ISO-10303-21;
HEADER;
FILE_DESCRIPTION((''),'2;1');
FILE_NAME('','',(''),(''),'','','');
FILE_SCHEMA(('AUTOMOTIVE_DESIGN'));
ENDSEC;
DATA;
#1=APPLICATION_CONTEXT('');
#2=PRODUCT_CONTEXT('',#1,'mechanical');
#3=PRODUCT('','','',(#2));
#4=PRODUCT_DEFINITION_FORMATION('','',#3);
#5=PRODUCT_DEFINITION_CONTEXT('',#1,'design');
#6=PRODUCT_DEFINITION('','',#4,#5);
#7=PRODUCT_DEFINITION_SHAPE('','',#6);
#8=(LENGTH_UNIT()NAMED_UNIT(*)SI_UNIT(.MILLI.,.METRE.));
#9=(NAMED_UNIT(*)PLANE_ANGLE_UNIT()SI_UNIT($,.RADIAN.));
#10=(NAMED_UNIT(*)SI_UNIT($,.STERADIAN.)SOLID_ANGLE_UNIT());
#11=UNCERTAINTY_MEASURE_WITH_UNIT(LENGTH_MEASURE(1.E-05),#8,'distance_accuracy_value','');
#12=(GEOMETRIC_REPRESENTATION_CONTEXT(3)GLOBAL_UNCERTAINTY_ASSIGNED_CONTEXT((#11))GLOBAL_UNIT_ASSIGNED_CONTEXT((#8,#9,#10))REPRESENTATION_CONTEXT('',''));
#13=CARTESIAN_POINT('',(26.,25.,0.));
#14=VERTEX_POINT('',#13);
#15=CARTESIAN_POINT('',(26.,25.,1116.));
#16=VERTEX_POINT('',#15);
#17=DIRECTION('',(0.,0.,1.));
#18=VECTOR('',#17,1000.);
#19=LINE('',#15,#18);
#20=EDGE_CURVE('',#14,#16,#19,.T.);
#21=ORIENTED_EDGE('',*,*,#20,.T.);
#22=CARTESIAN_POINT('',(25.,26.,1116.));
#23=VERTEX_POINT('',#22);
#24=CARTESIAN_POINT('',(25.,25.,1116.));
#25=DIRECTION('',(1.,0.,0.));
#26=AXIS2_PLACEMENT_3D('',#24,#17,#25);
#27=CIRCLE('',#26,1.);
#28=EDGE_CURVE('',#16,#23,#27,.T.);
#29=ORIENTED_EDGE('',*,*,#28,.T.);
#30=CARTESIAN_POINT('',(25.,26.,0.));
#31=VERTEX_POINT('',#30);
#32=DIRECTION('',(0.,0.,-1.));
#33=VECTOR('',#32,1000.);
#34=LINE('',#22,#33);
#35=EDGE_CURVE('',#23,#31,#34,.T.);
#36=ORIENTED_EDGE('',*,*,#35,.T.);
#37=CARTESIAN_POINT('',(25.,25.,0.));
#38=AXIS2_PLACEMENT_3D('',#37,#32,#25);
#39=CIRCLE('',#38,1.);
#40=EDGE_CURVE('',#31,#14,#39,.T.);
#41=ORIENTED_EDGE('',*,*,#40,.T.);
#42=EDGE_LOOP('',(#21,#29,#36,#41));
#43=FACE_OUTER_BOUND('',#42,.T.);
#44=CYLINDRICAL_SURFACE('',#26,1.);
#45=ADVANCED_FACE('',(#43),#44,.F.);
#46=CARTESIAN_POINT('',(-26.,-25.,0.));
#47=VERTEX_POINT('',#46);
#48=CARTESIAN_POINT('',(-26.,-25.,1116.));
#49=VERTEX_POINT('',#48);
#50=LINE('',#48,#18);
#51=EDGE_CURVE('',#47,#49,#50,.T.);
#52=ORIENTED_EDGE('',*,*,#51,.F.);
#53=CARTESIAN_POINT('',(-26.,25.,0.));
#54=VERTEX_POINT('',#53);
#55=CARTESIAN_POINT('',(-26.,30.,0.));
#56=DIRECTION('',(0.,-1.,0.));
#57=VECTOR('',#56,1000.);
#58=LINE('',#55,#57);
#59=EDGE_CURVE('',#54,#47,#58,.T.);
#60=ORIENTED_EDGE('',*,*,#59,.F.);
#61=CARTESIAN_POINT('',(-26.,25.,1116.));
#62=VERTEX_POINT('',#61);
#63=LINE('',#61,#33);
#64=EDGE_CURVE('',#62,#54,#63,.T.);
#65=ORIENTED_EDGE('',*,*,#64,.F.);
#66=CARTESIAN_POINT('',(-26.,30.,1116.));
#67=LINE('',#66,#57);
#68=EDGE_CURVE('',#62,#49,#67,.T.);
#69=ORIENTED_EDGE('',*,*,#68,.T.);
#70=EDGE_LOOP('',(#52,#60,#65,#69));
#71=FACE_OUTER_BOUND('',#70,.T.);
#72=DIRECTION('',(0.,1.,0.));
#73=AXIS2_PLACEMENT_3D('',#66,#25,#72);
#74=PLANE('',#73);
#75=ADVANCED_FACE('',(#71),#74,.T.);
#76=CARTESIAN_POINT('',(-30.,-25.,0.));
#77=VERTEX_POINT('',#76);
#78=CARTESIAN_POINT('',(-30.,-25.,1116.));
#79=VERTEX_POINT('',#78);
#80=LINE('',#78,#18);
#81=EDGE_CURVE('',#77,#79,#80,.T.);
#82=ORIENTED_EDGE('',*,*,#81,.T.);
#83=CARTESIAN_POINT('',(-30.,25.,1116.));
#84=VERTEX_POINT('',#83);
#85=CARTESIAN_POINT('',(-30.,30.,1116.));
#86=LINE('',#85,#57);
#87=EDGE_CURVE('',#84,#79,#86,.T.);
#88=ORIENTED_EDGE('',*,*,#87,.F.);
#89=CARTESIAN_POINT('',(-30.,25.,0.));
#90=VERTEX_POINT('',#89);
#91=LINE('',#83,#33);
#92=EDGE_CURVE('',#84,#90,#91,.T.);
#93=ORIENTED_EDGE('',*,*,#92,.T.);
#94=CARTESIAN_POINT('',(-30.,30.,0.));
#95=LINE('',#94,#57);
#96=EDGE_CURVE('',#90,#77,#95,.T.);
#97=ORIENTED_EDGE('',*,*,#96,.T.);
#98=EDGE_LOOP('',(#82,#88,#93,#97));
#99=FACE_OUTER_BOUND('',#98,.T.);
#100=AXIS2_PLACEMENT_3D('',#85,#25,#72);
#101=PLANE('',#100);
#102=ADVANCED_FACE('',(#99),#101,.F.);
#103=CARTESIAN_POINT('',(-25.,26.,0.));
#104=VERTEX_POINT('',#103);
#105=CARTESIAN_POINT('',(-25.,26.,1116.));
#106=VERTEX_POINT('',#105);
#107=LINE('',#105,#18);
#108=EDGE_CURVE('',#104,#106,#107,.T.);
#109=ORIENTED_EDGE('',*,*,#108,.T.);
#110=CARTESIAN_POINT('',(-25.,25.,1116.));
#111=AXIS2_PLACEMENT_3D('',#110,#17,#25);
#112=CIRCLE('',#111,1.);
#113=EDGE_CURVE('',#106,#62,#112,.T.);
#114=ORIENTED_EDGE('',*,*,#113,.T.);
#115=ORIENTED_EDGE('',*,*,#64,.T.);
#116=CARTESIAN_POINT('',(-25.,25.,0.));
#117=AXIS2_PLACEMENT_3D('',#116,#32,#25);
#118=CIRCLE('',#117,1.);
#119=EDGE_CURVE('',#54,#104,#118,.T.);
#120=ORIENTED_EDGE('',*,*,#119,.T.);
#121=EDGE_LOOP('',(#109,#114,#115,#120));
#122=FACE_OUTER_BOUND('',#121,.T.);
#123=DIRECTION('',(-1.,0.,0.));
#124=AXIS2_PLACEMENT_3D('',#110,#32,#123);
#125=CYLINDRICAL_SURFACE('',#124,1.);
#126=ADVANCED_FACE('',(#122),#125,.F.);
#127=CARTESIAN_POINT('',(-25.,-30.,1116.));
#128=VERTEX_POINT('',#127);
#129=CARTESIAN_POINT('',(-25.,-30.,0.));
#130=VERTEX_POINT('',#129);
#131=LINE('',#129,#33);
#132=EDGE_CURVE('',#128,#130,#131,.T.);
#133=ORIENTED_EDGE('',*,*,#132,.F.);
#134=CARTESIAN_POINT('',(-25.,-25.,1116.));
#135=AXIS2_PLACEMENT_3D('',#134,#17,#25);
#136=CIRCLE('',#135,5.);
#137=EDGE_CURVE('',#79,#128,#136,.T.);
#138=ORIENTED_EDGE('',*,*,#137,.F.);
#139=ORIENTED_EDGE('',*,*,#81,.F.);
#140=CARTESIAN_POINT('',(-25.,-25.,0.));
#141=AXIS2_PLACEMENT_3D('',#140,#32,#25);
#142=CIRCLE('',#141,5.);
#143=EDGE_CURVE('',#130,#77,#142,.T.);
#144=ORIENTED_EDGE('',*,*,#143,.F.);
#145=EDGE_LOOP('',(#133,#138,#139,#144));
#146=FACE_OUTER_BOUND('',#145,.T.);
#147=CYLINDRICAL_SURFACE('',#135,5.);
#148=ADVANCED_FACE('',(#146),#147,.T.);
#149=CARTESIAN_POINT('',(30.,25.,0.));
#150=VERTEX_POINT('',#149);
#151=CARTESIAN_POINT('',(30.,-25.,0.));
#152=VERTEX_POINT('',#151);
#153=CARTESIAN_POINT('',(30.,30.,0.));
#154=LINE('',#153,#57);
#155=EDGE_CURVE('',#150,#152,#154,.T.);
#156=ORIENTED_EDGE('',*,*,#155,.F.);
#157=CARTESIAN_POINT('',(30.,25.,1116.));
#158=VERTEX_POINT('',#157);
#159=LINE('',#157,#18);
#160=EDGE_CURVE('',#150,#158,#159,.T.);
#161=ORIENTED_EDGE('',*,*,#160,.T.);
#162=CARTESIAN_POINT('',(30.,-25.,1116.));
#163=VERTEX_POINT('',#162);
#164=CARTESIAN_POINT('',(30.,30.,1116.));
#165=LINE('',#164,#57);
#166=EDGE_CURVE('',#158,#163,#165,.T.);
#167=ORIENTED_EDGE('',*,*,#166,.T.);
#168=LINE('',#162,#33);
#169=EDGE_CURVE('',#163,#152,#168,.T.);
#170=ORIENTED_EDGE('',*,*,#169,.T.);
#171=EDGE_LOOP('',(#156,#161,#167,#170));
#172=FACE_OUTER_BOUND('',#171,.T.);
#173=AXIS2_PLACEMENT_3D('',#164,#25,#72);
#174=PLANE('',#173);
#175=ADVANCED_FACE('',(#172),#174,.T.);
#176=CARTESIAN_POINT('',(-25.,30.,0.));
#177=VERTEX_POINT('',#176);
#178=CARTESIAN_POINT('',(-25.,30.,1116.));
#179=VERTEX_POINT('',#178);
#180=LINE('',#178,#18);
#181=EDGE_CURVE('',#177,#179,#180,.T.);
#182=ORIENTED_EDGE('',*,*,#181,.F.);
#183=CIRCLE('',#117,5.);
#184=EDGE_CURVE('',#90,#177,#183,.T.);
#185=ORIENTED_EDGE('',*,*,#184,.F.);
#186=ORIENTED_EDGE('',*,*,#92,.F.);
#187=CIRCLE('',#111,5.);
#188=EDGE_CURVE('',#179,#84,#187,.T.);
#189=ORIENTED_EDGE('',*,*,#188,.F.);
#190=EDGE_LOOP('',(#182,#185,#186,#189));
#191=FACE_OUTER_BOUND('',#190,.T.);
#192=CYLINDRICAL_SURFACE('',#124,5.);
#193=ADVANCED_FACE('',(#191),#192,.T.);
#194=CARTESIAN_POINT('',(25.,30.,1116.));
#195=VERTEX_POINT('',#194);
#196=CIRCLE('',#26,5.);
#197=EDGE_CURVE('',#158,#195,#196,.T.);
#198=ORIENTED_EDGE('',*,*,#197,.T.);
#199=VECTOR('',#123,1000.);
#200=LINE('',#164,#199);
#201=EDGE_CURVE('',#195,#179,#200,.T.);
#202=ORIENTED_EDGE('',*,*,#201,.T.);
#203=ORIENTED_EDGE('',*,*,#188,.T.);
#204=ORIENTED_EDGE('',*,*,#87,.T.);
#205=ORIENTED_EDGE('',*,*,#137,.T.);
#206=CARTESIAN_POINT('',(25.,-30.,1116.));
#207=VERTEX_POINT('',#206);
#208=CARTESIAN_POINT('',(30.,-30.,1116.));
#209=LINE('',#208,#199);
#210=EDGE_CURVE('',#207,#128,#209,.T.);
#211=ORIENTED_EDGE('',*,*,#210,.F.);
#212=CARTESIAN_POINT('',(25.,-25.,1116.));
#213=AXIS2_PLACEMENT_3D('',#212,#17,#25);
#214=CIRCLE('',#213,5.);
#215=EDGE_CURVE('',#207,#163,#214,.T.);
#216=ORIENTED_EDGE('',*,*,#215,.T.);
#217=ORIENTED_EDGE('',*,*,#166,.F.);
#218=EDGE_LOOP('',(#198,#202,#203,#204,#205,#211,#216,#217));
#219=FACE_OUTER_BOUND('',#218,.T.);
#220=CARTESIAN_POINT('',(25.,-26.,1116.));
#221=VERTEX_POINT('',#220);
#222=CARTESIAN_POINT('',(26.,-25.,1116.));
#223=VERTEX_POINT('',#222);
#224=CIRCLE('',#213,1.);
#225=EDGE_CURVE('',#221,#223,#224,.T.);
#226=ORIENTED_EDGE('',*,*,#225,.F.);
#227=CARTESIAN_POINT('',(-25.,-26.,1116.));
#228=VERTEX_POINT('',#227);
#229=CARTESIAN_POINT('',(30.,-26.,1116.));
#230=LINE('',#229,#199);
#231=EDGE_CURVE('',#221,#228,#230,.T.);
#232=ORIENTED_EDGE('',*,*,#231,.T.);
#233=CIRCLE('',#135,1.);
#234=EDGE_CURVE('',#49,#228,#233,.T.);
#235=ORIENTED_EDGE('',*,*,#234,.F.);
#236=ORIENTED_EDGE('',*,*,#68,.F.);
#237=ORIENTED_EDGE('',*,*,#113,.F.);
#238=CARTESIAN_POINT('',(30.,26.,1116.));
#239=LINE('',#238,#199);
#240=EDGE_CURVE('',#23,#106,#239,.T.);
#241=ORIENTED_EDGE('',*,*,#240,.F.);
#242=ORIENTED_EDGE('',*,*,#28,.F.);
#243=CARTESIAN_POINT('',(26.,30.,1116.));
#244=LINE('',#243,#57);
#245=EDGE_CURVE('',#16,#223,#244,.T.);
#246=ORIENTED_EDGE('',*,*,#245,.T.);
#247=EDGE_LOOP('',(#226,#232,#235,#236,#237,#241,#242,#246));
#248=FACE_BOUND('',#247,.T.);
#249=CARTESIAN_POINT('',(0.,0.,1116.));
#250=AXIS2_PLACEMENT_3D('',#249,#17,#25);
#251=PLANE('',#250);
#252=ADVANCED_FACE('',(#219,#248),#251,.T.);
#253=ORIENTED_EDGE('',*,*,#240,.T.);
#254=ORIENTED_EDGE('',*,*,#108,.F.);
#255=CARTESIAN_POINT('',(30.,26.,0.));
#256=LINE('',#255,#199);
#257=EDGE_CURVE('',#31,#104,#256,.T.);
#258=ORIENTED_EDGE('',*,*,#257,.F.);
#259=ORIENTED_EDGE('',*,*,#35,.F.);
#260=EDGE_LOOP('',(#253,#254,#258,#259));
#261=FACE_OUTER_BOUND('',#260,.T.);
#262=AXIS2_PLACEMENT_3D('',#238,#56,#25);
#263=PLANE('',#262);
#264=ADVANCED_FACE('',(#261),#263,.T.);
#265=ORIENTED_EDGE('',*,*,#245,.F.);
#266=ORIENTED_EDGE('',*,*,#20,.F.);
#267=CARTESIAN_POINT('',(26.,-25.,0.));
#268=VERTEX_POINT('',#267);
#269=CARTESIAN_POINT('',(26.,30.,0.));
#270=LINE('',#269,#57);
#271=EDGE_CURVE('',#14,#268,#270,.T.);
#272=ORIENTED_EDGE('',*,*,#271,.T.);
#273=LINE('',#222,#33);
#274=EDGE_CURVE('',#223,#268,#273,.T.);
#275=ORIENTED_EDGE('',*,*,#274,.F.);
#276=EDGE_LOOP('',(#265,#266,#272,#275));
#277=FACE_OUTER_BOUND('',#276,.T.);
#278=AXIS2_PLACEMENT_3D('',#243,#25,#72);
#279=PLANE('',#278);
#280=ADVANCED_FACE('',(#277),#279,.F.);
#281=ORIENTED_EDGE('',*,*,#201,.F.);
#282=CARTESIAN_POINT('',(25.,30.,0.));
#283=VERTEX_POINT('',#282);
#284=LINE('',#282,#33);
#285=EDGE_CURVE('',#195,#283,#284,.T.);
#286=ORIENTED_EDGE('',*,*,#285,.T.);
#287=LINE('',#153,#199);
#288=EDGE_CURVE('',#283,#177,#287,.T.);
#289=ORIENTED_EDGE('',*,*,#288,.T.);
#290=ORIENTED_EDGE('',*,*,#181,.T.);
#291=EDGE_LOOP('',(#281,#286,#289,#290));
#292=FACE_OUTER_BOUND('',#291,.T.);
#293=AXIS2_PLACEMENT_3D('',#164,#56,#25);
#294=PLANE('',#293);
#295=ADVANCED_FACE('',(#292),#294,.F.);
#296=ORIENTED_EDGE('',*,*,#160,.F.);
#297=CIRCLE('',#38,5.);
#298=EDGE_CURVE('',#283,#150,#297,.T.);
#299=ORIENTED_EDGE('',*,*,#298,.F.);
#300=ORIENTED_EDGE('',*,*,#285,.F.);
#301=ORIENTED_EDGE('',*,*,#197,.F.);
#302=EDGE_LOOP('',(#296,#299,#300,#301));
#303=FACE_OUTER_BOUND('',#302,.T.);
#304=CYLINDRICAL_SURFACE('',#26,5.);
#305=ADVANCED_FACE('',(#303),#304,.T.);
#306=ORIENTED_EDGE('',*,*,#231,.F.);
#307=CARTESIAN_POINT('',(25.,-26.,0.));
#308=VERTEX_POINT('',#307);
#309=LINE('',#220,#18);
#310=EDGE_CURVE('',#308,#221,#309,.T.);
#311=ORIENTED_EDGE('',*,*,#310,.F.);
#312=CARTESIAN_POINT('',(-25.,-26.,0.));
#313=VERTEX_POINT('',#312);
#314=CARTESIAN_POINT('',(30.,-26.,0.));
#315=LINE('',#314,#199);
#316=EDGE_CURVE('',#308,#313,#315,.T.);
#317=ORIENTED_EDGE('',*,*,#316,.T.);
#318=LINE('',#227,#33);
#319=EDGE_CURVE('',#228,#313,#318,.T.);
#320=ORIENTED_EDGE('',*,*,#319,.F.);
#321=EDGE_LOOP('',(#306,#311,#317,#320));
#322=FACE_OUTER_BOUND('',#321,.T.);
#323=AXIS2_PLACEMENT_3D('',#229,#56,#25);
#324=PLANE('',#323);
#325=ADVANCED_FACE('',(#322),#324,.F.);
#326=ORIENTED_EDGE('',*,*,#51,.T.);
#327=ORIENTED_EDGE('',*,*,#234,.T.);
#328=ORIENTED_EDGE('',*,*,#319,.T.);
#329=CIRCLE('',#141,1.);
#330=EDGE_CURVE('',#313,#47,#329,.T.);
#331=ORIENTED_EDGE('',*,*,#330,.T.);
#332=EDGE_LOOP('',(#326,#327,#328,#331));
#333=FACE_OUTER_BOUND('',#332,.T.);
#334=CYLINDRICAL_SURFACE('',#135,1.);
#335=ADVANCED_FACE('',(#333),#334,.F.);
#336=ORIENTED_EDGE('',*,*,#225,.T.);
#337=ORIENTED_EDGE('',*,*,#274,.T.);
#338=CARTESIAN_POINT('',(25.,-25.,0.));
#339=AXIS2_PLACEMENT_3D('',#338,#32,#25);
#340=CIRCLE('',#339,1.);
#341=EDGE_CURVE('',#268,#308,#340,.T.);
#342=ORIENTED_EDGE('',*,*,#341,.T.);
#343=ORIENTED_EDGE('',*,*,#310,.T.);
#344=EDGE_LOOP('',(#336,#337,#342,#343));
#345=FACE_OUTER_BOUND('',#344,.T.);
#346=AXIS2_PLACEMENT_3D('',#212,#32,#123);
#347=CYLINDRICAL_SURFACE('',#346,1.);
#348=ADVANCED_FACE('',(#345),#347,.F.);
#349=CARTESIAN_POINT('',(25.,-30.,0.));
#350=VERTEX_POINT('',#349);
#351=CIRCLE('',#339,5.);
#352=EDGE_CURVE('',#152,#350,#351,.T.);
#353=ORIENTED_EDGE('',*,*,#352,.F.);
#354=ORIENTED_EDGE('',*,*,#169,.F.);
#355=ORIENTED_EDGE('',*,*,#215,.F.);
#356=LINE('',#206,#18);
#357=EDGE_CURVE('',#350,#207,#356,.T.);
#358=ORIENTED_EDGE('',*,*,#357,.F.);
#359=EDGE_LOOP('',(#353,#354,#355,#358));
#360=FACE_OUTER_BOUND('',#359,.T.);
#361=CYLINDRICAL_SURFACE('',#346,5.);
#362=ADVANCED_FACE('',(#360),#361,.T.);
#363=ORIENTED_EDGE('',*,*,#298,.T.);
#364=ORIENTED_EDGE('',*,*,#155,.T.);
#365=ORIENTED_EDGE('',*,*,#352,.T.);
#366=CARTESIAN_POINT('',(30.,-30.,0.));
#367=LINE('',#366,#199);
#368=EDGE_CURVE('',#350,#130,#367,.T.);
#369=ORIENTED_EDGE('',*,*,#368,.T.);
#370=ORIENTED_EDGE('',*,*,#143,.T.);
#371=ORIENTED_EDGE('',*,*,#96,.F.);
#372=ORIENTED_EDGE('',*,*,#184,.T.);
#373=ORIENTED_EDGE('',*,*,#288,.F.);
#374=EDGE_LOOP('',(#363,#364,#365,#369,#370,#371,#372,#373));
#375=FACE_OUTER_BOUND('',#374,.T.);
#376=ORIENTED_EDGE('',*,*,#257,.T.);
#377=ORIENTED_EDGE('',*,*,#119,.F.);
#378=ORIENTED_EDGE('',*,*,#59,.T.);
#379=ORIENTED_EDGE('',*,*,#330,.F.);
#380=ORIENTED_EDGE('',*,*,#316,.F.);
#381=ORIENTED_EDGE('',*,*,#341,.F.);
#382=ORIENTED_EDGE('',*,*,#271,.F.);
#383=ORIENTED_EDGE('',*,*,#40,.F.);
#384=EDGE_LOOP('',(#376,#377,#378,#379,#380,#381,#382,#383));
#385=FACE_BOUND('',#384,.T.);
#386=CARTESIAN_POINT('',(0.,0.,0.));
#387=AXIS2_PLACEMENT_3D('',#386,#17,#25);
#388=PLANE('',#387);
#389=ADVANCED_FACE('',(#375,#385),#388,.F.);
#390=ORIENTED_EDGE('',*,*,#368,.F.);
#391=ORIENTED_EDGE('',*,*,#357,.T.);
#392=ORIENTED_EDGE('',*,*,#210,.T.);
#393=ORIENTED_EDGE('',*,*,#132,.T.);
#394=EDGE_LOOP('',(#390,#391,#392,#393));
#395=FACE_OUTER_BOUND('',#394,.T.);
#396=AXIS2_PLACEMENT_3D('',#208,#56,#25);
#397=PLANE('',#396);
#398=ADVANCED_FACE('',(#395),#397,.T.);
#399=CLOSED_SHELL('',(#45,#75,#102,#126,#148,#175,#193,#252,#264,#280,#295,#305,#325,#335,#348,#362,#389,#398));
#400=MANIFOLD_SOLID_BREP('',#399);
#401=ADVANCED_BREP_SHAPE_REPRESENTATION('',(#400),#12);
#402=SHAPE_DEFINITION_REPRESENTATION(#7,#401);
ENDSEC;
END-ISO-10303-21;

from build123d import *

# Parameters (mm, degrees)
SKETCH1_W           = 60
SKETCH1_H           = 60
BOSS_EXTRUDE1_DEPTH = 1116
FILLET1_R           = 5
SHELL1_T            = -4


with BuildPart() as part:
    # Sketch1 → Boss-Extrude1 (new body)
    with BuildSketch(Plane.XY):
        Rectangle(SKETCH1_W, SKETCH1_H)
    extrude(amount=BOSS_EXTRUDE1_DEPTH)

    # Fillet1
    fillet1_edges = [part.edges().sort_by_distance(p)[0] for p in [
        (30, -30, 558),
        (30, 30, 558),
        (-30, 30, 558),
        (-30, -30, 558),
    ]]
    fillet(fillet1_edges, radius=FILLET1_R)

    # Shell1
    shell1_openings = [part.faces().sort_by_distance(p)[0] for p in [
        (0, 0, 1116),
        (0, 0, 0),
    ]]
    offset(amount=SHELL1_T, openings=shell1_openings, kind=Kind.INTERSECTION)


solid = part.part
